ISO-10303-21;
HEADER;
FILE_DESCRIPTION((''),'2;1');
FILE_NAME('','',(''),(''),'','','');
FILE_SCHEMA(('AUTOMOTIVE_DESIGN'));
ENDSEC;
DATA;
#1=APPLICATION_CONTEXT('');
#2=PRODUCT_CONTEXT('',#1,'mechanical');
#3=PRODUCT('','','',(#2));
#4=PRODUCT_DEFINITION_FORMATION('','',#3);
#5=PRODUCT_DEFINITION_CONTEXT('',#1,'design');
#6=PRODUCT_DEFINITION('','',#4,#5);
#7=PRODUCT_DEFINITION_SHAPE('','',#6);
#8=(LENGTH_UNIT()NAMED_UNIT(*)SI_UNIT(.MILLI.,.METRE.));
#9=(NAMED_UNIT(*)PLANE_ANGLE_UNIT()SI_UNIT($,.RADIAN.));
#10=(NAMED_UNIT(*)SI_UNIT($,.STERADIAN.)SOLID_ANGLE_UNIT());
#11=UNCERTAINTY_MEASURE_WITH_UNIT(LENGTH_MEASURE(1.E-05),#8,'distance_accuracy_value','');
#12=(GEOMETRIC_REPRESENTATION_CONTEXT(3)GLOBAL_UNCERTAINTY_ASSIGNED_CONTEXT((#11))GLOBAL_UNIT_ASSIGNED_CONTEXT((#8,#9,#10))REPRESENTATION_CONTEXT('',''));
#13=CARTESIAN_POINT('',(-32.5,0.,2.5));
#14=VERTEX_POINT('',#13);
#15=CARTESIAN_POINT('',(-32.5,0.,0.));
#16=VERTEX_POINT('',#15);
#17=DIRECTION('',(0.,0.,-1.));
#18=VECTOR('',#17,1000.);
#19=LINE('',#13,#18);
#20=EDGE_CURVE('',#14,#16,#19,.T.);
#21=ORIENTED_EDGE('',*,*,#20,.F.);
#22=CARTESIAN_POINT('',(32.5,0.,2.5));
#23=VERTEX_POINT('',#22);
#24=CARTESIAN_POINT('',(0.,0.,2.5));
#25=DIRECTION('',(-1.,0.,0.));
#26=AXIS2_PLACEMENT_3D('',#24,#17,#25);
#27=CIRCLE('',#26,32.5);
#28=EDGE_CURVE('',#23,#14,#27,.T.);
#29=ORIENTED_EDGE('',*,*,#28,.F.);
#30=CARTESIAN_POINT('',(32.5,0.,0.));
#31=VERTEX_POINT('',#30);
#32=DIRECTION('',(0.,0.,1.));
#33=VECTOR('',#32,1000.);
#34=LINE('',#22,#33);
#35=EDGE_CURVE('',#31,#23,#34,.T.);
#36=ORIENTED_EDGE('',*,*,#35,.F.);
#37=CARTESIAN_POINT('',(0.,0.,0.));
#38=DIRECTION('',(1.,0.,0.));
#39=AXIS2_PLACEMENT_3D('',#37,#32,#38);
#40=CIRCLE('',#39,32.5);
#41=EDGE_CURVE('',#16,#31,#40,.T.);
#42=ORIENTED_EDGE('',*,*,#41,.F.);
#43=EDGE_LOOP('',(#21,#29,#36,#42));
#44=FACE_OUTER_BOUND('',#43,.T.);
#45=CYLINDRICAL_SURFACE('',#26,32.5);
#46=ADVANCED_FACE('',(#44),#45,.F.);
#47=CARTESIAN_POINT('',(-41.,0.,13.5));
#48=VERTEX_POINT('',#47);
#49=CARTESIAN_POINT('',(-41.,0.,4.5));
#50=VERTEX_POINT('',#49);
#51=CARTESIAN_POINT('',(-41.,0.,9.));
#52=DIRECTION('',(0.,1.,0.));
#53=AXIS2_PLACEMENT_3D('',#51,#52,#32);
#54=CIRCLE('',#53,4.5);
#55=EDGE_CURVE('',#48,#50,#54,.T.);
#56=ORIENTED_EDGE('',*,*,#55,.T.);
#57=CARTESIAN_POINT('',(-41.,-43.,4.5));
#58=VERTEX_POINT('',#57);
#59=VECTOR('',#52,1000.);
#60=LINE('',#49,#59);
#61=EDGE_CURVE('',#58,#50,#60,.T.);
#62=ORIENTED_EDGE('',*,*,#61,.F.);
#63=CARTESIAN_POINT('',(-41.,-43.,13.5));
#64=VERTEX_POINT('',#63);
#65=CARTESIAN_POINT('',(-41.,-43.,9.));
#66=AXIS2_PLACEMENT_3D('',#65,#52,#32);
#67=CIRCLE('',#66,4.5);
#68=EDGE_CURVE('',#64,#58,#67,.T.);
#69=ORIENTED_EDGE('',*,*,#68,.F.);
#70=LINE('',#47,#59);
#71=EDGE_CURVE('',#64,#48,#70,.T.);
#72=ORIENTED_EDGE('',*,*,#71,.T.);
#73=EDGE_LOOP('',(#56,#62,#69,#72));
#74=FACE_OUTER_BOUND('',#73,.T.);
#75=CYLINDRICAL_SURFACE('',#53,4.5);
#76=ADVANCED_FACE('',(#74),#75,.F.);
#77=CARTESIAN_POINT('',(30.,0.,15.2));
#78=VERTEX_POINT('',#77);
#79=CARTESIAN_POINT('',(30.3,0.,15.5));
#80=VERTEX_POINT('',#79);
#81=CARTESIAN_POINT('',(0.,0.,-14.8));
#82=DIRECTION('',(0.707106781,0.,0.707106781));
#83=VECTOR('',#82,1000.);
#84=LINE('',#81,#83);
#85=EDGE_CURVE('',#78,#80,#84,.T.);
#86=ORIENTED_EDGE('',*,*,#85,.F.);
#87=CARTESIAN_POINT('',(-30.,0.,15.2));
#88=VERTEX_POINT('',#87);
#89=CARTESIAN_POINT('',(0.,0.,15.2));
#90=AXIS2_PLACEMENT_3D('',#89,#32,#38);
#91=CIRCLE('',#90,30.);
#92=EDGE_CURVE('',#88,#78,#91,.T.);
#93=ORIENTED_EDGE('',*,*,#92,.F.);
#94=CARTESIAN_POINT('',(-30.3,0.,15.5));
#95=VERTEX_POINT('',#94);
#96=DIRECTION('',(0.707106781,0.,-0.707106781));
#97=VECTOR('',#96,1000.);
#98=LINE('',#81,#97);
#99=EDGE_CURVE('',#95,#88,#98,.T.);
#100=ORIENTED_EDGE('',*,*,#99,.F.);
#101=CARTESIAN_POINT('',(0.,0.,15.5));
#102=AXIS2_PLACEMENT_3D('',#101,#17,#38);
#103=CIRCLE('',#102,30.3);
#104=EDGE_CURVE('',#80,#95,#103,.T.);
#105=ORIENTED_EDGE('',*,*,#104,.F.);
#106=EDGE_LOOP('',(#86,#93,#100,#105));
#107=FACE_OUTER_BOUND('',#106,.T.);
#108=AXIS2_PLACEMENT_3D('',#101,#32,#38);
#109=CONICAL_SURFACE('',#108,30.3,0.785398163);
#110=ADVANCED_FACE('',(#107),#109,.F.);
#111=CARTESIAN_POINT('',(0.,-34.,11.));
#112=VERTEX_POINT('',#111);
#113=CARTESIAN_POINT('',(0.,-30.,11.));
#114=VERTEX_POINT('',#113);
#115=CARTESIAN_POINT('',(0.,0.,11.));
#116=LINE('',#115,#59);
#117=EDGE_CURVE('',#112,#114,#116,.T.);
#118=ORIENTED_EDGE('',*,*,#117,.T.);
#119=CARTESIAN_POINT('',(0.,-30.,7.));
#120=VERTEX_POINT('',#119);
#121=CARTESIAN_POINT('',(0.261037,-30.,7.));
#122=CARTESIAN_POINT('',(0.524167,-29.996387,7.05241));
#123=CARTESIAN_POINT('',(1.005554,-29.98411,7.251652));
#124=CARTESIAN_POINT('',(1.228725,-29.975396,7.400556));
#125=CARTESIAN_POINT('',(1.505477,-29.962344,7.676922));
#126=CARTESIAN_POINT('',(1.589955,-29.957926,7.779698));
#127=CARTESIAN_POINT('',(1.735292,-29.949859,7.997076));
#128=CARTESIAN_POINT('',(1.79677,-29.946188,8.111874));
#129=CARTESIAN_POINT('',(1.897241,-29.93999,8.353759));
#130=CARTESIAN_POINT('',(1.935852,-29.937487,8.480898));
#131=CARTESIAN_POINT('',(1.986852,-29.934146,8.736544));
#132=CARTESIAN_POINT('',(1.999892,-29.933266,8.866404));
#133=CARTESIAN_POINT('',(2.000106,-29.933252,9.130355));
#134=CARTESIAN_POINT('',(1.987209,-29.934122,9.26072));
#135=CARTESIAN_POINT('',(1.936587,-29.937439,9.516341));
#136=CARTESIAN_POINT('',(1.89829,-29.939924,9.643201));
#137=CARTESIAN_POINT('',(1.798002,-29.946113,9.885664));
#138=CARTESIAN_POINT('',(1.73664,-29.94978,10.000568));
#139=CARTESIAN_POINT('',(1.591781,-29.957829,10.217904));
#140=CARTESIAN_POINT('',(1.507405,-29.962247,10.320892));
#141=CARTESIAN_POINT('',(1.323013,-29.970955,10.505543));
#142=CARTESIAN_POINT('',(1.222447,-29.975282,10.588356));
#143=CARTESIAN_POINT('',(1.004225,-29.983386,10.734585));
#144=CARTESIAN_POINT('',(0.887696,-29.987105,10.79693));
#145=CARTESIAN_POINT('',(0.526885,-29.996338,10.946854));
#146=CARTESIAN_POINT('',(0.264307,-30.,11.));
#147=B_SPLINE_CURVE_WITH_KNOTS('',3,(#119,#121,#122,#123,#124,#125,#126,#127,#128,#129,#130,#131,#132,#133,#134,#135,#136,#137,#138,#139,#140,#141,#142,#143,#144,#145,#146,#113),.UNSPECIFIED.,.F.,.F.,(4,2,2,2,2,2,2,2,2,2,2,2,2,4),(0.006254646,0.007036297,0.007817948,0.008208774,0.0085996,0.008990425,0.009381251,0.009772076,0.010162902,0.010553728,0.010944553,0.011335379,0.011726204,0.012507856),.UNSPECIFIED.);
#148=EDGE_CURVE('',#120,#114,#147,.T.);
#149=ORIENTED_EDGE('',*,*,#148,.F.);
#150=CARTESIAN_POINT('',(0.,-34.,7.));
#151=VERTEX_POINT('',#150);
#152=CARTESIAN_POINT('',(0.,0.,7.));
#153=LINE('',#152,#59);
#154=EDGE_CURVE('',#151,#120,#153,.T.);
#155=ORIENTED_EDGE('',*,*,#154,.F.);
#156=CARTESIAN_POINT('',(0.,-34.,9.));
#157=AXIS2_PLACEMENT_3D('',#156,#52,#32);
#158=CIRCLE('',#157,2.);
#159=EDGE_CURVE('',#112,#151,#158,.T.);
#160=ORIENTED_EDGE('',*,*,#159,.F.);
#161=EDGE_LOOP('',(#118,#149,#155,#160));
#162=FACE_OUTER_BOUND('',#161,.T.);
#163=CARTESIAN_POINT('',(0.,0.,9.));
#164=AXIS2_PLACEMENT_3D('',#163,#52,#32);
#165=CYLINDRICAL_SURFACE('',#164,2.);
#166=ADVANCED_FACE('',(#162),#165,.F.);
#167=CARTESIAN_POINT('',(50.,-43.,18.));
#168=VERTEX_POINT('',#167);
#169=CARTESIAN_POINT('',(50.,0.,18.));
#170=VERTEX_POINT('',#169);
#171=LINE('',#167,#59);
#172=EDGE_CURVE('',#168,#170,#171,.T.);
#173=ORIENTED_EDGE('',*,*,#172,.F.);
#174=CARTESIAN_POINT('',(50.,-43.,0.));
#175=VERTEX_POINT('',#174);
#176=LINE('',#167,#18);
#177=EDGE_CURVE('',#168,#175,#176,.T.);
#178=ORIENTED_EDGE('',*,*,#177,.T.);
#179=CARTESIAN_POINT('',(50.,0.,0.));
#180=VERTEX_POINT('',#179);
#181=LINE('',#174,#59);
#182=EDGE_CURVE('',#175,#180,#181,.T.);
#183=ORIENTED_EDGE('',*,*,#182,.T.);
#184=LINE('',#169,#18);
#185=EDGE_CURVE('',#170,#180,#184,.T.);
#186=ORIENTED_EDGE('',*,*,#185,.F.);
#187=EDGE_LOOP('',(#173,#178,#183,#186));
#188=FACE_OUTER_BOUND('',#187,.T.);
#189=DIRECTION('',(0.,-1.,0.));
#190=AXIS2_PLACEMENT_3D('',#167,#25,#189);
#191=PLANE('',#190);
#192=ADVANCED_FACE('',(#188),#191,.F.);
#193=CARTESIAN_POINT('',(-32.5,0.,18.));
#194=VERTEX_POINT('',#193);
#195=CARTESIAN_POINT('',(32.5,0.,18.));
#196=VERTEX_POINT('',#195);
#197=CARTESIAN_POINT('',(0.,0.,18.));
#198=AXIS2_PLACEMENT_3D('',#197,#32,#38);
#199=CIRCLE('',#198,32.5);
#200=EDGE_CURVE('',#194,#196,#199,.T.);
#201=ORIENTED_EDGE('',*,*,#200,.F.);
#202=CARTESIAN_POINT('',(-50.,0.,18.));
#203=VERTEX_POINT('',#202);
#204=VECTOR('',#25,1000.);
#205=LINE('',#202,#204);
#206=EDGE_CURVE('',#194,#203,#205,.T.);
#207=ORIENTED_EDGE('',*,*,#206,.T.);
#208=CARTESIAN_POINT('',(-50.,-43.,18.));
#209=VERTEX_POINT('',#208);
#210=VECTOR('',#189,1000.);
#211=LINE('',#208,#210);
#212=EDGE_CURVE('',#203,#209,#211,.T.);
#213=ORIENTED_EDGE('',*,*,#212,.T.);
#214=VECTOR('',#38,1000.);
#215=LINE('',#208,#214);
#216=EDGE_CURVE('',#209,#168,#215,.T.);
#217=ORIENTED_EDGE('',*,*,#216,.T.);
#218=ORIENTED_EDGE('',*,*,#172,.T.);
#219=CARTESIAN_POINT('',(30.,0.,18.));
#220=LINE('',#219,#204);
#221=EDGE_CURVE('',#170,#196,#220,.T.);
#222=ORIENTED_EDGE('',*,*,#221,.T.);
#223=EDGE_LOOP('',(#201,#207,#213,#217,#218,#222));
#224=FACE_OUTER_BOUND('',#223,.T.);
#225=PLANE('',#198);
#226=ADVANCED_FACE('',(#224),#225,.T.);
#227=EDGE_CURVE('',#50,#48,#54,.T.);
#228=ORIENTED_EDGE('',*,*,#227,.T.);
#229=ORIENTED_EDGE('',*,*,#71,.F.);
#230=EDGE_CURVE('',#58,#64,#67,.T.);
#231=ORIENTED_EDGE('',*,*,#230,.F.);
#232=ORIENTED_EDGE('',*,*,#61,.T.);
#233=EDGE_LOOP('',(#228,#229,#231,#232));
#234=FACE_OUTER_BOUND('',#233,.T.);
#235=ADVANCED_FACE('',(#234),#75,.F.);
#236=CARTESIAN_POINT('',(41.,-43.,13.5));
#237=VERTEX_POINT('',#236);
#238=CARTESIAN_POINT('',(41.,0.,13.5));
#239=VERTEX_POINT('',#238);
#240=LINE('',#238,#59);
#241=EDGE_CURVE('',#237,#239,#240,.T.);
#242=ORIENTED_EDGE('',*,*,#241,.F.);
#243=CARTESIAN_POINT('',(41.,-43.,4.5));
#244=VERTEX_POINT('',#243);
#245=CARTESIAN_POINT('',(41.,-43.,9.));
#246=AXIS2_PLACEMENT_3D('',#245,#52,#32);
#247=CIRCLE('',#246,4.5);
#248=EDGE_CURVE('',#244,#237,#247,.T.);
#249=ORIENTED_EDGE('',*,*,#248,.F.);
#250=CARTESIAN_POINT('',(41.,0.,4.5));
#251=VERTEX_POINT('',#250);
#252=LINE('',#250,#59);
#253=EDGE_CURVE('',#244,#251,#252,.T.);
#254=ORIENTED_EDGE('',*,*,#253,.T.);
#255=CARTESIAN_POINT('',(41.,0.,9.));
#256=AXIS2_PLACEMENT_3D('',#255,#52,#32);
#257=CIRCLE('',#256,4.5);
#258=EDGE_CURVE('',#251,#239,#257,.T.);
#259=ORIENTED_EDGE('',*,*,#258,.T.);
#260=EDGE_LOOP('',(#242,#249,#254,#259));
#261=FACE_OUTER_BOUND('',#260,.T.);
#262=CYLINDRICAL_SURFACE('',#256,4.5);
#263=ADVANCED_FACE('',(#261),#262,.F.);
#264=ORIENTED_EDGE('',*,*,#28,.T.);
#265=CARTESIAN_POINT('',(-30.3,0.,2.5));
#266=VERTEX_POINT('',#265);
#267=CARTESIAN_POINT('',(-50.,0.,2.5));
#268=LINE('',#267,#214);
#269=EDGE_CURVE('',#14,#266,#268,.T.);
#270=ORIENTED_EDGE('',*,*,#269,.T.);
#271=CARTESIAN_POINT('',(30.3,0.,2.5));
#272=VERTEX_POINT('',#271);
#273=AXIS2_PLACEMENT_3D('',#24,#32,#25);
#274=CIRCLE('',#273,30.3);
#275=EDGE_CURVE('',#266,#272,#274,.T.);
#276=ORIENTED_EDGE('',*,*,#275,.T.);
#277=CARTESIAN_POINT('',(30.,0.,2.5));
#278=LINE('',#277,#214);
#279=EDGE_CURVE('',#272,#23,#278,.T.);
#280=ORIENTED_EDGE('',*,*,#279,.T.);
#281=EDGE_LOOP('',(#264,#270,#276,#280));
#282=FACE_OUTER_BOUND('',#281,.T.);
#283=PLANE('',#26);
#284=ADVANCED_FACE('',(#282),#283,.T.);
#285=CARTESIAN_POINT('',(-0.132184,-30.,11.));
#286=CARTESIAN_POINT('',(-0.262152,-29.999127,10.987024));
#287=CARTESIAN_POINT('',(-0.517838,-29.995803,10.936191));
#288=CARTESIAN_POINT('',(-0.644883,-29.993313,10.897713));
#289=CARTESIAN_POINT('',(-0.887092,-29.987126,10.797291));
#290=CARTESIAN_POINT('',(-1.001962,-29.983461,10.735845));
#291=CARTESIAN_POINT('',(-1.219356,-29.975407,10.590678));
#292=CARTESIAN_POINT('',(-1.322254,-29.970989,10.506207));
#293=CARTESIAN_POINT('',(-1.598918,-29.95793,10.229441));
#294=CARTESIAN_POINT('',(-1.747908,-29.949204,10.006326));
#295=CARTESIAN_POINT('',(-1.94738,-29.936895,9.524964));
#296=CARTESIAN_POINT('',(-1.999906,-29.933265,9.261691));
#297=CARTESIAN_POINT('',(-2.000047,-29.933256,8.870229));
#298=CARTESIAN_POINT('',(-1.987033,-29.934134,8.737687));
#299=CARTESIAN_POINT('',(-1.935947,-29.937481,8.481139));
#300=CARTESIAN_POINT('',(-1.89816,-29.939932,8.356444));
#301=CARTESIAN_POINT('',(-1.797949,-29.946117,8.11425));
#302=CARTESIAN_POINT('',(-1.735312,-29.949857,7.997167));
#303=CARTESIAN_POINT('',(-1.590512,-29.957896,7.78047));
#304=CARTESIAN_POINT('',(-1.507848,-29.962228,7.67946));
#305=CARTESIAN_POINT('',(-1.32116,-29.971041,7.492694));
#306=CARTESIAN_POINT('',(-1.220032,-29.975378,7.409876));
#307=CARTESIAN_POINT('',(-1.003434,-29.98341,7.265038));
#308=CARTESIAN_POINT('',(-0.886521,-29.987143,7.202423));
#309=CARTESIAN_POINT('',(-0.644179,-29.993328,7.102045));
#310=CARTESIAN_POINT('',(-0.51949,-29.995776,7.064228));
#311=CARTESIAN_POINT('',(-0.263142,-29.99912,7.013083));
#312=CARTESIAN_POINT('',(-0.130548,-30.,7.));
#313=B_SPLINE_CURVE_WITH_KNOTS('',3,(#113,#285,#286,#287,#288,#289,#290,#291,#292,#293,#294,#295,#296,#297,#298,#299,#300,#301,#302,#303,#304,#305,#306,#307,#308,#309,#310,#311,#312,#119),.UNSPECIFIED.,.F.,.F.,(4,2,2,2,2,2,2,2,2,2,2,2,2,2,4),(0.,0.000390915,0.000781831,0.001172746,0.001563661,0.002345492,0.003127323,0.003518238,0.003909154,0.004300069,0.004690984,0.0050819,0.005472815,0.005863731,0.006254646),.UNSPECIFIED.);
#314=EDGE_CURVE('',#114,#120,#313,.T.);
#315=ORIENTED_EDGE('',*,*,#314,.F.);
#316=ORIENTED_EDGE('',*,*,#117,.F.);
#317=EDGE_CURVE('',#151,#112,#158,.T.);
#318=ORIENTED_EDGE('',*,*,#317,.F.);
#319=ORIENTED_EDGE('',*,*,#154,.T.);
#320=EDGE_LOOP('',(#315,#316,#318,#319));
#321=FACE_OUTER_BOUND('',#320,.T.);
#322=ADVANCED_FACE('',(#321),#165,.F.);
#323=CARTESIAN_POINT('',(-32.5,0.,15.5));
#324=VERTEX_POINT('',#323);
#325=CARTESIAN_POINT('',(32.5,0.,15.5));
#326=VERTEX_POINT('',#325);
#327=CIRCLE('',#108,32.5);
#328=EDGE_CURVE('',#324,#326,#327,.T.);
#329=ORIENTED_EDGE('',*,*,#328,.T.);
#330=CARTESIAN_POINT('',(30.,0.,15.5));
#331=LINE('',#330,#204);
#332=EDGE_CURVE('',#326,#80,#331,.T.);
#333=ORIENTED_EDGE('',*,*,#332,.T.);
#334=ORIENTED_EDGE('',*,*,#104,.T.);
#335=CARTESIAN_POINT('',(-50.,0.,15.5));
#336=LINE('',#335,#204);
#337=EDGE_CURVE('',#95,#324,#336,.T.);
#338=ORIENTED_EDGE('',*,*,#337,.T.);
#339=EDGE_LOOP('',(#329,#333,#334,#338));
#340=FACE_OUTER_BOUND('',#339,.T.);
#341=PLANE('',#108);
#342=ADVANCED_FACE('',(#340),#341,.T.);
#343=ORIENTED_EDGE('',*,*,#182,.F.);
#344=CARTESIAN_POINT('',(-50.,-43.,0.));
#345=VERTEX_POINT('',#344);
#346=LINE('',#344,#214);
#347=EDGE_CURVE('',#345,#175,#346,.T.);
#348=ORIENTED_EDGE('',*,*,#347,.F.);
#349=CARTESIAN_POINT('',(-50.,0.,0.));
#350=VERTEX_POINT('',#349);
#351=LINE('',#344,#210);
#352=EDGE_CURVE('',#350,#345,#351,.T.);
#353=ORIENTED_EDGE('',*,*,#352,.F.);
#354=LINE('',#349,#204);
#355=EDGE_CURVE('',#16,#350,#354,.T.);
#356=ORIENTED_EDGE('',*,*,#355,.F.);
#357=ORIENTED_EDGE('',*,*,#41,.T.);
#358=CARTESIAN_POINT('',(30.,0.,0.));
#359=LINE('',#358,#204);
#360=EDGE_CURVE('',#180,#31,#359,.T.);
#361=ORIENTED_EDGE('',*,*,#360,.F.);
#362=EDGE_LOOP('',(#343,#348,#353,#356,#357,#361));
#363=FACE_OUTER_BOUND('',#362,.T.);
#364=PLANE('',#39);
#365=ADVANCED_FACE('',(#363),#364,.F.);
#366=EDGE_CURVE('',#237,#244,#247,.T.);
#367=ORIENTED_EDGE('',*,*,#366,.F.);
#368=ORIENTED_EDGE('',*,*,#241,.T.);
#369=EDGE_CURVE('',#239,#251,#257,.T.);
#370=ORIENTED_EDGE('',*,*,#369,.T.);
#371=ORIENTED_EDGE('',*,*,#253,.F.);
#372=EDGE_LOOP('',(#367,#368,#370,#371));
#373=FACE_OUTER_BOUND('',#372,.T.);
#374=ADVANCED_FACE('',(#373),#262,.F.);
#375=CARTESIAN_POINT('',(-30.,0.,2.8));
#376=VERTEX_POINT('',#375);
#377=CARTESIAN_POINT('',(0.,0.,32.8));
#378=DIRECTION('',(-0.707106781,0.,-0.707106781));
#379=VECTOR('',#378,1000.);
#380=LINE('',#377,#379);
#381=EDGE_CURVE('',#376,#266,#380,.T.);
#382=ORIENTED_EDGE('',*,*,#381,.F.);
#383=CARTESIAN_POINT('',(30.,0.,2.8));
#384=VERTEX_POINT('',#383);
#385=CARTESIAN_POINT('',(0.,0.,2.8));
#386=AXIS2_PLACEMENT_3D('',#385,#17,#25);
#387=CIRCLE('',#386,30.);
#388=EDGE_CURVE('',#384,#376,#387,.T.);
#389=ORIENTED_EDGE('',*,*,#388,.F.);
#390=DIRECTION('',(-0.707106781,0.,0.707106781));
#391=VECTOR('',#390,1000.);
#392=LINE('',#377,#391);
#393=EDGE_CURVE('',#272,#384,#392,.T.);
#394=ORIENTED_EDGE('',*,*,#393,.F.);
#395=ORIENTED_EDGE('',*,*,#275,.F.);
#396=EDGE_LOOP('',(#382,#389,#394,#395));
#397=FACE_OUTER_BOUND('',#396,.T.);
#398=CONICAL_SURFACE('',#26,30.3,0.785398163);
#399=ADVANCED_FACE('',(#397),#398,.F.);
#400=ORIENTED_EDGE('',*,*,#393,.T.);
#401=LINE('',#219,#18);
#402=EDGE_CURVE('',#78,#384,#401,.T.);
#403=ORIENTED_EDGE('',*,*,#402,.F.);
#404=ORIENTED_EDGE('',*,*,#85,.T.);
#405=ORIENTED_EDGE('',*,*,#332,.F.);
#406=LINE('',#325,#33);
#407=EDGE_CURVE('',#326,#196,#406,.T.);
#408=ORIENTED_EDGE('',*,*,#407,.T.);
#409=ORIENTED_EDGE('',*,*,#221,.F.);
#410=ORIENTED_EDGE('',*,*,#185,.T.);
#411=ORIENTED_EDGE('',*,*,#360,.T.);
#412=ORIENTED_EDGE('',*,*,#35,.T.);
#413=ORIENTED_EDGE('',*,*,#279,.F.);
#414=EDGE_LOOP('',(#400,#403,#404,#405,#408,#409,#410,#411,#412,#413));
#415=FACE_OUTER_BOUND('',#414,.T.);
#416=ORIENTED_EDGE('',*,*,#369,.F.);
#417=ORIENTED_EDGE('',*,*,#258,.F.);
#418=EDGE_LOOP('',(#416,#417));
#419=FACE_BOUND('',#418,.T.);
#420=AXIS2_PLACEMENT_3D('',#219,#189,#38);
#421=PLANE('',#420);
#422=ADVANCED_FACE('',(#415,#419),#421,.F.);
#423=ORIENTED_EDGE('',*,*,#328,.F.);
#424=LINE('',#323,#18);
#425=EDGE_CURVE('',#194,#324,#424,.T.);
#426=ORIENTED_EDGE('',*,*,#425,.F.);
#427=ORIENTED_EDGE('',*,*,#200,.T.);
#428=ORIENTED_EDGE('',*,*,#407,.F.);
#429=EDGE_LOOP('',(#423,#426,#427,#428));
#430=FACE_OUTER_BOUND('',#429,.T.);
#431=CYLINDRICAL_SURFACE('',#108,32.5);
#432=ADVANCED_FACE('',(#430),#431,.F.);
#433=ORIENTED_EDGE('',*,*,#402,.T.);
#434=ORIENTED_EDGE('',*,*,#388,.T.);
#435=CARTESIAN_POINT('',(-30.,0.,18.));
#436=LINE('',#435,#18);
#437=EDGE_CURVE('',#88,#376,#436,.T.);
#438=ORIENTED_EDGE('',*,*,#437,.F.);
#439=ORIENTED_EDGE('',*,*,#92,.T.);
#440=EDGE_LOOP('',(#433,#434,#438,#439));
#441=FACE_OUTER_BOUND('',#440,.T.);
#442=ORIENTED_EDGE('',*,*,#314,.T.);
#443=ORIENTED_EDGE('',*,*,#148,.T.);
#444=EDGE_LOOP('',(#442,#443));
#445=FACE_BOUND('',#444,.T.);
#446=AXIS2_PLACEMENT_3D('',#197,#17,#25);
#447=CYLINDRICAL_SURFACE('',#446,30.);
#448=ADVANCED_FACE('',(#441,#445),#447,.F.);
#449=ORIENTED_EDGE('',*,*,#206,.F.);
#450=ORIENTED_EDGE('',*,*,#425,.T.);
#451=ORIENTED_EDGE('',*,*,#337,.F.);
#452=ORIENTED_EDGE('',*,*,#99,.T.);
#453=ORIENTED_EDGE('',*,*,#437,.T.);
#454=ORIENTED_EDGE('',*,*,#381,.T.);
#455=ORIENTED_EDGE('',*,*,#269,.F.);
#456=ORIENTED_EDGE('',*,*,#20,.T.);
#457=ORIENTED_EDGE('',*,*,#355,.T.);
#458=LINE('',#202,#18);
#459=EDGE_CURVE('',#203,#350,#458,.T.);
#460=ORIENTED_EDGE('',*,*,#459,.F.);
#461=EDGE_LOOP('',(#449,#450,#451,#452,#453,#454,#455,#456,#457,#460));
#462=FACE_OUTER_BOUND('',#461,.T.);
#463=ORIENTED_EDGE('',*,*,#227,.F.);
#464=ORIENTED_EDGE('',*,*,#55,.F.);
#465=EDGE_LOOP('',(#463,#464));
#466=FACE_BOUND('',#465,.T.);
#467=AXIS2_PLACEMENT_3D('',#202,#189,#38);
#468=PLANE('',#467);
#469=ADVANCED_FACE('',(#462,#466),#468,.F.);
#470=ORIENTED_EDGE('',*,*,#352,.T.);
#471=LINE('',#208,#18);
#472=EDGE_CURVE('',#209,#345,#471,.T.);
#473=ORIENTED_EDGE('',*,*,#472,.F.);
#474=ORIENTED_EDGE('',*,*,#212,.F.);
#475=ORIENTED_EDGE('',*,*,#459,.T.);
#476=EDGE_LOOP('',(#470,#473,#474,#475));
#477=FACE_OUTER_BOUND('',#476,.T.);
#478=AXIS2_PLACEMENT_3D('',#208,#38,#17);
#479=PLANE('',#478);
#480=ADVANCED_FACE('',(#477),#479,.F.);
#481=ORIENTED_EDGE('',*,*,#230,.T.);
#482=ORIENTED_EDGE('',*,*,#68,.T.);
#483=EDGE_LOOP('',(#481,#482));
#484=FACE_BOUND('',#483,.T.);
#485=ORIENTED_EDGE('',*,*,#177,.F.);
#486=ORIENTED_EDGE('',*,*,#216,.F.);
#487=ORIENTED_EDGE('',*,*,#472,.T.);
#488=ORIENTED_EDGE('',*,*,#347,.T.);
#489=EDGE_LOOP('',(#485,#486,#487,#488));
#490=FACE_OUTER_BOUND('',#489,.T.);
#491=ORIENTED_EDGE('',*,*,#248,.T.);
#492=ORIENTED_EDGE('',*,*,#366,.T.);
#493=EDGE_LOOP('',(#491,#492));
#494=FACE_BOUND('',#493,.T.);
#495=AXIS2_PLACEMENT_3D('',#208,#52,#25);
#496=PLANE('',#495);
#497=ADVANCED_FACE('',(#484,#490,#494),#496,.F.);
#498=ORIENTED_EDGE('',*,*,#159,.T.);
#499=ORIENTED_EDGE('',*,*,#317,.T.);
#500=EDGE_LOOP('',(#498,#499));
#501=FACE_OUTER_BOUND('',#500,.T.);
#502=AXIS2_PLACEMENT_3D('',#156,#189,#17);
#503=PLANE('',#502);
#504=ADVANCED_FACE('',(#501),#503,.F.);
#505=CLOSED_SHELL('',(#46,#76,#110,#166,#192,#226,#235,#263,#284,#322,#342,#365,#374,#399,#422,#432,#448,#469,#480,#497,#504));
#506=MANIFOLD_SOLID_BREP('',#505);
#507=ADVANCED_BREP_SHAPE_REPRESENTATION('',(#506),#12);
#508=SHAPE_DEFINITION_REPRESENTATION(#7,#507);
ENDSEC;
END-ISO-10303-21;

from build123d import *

# Parameters (mm, degrees)
BOSS_EXTRUDE1_DEPTH = 18
SKETCH2_R           = 32.5
CUT_EXTRUDE1_DEPTH  = 2.5
CUT_EXTRUDE2_START  = -2.5
SKETCH3_R           = 32.5
CUT_EXTRUDE2_DEPTH  = 2.5
CHAMFER1_SIZE       = 0.3
HOLE1_D             = 9
HOLE2_D             = 4
HOLE2_DEPTH         = 34


with BuildPart() as part:
    # Sketch1 → Boss-Extrude1 (new body)
    with BuildSketch(Plane.XY):
        with BuildLine():
            Line((-50, 0), (-30, 0))
            ThreePointArc((-30, 0), (0, -30), (30, 0))
            Line((30, 0), (50, 0))
            Line((50, 0), (50, -43))
            Line((50, -43), (-50, -43))
            Line((-50, -43), (-50, 0))
        make_face()
    extrude(amount=BOSS_EXTRUDE1_DEPTH)

    # Sketch2 → Cut-Extrude1 (cut)
    with BuildSketch(Plane.XY.offset(18)):
        Circle(SKETCH2_R)
    extrude(amount=-CUT_EXTRUDE1_DEPTH, mode=Mode.SUBTRACT)

    # Sketch3 → Cut-Extrude2 (cut)
    with BuildSketch(Plane(origin=(0, 0, 0), x_dir=(-1, 0, 0), z_dir=(0, 0, -1)).offset(CUT_EXTRUDE2_START)):
        Circle(SKETCH3_R)
    extrude(amount=CUT_EXTRUDE2_DEPTH, mode=Mode.SUBTRACT)

    # Chamfer1
    chamfer1_edges = [part.edges().sort_by_distance(p)[0] for p in [
        (0, -30, 15.5),
        (0, -30, 2.5),
    ]]
    chamfer(chamfer1_edges, length=CHAMFER1_SIZE)

    # Hole1 (through all)
    with Locations(Plane(origin=(0, 0, 0), x_dir=(1, 0, 0), z_dir=(0, 1, 0))):
        with Locations((-41, -9), (41, -9)):
            Hole(HOLE1_D / 2)

    # Hole2
    with Locations(Plane(origin=(0, 0, 0), x_dir=(1, 0, 0), z_dir=(0, 1, 0))):
        with Locations((0, -9)):
            Hole(HOLE2_D / 2, depth=HOLE2_DEPTH)


solid = part.part
